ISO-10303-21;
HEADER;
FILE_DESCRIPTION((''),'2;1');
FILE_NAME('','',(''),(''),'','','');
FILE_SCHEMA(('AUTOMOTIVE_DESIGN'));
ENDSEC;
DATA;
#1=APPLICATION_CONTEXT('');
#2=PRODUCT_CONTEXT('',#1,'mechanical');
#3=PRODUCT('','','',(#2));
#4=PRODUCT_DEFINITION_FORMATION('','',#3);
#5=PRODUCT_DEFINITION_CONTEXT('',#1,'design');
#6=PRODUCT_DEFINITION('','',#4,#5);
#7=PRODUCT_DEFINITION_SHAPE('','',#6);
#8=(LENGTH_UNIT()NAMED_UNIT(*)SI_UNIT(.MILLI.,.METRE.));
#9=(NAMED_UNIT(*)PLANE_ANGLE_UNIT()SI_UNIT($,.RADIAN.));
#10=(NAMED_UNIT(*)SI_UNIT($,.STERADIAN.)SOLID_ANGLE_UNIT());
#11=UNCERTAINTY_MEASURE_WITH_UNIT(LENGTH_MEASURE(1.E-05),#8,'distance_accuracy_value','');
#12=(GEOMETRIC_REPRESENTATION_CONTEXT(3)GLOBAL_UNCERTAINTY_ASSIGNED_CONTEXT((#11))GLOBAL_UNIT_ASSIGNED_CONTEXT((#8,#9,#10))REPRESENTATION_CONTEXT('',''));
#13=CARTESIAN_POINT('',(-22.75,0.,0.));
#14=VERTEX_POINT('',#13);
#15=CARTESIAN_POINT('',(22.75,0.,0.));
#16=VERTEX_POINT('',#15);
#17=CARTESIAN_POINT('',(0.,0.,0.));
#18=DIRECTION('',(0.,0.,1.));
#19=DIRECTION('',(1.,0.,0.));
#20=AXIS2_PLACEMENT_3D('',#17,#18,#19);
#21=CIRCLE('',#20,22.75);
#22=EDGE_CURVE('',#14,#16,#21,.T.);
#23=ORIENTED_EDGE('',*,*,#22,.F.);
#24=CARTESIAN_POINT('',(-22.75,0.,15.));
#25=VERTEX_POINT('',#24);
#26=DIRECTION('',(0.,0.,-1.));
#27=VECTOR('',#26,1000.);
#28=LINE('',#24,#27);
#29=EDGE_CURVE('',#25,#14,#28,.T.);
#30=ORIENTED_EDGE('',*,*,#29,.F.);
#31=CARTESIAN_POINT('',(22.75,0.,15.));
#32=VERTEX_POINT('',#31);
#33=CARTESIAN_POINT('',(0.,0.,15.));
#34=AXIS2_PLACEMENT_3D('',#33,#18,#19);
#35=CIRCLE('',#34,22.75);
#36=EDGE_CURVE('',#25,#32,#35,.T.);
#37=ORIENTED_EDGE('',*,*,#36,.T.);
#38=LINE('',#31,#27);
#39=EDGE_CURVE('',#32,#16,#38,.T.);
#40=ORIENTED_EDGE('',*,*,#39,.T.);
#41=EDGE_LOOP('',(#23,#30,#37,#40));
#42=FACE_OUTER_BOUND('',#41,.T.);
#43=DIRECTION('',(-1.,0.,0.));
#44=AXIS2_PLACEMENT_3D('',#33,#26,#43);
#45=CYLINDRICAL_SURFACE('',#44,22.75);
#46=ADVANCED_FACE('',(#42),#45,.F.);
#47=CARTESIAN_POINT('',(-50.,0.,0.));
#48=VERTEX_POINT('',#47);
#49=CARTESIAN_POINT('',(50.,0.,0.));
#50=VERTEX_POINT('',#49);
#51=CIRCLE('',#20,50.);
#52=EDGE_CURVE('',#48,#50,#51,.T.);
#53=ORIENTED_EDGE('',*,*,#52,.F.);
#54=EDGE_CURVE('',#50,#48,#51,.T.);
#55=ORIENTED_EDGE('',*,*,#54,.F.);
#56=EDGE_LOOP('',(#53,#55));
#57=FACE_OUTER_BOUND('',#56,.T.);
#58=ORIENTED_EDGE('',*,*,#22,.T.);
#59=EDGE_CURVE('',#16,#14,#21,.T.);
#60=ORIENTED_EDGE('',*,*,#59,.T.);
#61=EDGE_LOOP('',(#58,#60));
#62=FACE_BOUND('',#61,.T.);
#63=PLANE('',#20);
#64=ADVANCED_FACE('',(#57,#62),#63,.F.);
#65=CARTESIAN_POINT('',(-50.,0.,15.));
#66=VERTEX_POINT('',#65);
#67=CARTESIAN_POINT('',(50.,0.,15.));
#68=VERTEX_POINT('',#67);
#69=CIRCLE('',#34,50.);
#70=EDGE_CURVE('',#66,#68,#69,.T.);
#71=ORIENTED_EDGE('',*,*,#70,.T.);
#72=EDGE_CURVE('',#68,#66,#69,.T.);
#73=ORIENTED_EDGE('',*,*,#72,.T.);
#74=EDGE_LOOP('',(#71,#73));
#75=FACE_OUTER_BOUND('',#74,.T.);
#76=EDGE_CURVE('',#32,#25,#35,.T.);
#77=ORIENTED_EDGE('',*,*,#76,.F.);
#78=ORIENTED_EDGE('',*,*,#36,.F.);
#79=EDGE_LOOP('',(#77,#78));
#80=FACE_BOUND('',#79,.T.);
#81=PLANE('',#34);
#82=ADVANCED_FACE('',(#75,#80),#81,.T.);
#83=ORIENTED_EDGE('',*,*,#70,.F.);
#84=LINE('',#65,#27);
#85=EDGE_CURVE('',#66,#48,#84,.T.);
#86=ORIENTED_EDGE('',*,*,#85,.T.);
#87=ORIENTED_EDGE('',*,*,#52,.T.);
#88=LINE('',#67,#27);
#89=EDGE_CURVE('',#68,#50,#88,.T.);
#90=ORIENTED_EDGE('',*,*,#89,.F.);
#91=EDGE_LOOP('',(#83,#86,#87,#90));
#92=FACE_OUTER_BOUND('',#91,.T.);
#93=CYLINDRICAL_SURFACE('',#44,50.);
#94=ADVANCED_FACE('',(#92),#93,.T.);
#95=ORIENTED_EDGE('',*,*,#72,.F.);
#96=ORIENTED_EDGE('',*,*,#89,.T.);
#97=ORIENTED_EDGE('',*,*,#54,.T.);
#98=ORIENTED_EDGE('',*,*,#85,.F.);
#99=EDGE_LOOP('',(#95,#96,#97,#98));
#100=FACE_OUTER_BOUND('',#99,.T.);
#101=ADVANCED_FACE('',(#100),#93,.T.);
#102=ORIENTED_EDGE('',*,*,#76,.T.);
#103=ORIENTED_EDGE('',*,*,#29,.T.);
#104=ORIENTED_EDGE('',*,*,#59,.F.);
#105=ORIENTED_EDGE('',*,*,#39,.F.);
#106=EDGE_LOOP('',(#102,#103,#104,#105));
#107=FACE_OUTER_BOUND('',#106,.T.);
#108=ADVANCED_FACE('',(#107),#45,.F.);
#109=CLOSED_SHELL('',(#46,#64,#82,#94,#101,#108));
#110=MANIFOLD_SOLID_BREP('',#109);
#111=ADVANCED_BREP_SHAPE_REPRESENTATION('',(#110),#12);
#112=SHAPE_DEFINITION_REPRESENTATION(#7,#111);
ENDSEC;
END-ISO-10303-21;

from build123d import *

# Parameters (mm, degrees)
SKETCH_1_R      = 50
SKETCH_1_R_2    = 22.75
EXTRUDE_1_DEPTH = 15


with BuildPart() as part:
    # 草图1 → 凸台-拉伸1 (new body)
    with BuildSketch(Plane.XY):
        Circle(SKETCH_1_R)
        Circle(SKETCH_1_R_2, mode=Mode.SUBTRACT)
    extrude(amount=EXTRUDE_1_DEPTH)


solid = part.part
